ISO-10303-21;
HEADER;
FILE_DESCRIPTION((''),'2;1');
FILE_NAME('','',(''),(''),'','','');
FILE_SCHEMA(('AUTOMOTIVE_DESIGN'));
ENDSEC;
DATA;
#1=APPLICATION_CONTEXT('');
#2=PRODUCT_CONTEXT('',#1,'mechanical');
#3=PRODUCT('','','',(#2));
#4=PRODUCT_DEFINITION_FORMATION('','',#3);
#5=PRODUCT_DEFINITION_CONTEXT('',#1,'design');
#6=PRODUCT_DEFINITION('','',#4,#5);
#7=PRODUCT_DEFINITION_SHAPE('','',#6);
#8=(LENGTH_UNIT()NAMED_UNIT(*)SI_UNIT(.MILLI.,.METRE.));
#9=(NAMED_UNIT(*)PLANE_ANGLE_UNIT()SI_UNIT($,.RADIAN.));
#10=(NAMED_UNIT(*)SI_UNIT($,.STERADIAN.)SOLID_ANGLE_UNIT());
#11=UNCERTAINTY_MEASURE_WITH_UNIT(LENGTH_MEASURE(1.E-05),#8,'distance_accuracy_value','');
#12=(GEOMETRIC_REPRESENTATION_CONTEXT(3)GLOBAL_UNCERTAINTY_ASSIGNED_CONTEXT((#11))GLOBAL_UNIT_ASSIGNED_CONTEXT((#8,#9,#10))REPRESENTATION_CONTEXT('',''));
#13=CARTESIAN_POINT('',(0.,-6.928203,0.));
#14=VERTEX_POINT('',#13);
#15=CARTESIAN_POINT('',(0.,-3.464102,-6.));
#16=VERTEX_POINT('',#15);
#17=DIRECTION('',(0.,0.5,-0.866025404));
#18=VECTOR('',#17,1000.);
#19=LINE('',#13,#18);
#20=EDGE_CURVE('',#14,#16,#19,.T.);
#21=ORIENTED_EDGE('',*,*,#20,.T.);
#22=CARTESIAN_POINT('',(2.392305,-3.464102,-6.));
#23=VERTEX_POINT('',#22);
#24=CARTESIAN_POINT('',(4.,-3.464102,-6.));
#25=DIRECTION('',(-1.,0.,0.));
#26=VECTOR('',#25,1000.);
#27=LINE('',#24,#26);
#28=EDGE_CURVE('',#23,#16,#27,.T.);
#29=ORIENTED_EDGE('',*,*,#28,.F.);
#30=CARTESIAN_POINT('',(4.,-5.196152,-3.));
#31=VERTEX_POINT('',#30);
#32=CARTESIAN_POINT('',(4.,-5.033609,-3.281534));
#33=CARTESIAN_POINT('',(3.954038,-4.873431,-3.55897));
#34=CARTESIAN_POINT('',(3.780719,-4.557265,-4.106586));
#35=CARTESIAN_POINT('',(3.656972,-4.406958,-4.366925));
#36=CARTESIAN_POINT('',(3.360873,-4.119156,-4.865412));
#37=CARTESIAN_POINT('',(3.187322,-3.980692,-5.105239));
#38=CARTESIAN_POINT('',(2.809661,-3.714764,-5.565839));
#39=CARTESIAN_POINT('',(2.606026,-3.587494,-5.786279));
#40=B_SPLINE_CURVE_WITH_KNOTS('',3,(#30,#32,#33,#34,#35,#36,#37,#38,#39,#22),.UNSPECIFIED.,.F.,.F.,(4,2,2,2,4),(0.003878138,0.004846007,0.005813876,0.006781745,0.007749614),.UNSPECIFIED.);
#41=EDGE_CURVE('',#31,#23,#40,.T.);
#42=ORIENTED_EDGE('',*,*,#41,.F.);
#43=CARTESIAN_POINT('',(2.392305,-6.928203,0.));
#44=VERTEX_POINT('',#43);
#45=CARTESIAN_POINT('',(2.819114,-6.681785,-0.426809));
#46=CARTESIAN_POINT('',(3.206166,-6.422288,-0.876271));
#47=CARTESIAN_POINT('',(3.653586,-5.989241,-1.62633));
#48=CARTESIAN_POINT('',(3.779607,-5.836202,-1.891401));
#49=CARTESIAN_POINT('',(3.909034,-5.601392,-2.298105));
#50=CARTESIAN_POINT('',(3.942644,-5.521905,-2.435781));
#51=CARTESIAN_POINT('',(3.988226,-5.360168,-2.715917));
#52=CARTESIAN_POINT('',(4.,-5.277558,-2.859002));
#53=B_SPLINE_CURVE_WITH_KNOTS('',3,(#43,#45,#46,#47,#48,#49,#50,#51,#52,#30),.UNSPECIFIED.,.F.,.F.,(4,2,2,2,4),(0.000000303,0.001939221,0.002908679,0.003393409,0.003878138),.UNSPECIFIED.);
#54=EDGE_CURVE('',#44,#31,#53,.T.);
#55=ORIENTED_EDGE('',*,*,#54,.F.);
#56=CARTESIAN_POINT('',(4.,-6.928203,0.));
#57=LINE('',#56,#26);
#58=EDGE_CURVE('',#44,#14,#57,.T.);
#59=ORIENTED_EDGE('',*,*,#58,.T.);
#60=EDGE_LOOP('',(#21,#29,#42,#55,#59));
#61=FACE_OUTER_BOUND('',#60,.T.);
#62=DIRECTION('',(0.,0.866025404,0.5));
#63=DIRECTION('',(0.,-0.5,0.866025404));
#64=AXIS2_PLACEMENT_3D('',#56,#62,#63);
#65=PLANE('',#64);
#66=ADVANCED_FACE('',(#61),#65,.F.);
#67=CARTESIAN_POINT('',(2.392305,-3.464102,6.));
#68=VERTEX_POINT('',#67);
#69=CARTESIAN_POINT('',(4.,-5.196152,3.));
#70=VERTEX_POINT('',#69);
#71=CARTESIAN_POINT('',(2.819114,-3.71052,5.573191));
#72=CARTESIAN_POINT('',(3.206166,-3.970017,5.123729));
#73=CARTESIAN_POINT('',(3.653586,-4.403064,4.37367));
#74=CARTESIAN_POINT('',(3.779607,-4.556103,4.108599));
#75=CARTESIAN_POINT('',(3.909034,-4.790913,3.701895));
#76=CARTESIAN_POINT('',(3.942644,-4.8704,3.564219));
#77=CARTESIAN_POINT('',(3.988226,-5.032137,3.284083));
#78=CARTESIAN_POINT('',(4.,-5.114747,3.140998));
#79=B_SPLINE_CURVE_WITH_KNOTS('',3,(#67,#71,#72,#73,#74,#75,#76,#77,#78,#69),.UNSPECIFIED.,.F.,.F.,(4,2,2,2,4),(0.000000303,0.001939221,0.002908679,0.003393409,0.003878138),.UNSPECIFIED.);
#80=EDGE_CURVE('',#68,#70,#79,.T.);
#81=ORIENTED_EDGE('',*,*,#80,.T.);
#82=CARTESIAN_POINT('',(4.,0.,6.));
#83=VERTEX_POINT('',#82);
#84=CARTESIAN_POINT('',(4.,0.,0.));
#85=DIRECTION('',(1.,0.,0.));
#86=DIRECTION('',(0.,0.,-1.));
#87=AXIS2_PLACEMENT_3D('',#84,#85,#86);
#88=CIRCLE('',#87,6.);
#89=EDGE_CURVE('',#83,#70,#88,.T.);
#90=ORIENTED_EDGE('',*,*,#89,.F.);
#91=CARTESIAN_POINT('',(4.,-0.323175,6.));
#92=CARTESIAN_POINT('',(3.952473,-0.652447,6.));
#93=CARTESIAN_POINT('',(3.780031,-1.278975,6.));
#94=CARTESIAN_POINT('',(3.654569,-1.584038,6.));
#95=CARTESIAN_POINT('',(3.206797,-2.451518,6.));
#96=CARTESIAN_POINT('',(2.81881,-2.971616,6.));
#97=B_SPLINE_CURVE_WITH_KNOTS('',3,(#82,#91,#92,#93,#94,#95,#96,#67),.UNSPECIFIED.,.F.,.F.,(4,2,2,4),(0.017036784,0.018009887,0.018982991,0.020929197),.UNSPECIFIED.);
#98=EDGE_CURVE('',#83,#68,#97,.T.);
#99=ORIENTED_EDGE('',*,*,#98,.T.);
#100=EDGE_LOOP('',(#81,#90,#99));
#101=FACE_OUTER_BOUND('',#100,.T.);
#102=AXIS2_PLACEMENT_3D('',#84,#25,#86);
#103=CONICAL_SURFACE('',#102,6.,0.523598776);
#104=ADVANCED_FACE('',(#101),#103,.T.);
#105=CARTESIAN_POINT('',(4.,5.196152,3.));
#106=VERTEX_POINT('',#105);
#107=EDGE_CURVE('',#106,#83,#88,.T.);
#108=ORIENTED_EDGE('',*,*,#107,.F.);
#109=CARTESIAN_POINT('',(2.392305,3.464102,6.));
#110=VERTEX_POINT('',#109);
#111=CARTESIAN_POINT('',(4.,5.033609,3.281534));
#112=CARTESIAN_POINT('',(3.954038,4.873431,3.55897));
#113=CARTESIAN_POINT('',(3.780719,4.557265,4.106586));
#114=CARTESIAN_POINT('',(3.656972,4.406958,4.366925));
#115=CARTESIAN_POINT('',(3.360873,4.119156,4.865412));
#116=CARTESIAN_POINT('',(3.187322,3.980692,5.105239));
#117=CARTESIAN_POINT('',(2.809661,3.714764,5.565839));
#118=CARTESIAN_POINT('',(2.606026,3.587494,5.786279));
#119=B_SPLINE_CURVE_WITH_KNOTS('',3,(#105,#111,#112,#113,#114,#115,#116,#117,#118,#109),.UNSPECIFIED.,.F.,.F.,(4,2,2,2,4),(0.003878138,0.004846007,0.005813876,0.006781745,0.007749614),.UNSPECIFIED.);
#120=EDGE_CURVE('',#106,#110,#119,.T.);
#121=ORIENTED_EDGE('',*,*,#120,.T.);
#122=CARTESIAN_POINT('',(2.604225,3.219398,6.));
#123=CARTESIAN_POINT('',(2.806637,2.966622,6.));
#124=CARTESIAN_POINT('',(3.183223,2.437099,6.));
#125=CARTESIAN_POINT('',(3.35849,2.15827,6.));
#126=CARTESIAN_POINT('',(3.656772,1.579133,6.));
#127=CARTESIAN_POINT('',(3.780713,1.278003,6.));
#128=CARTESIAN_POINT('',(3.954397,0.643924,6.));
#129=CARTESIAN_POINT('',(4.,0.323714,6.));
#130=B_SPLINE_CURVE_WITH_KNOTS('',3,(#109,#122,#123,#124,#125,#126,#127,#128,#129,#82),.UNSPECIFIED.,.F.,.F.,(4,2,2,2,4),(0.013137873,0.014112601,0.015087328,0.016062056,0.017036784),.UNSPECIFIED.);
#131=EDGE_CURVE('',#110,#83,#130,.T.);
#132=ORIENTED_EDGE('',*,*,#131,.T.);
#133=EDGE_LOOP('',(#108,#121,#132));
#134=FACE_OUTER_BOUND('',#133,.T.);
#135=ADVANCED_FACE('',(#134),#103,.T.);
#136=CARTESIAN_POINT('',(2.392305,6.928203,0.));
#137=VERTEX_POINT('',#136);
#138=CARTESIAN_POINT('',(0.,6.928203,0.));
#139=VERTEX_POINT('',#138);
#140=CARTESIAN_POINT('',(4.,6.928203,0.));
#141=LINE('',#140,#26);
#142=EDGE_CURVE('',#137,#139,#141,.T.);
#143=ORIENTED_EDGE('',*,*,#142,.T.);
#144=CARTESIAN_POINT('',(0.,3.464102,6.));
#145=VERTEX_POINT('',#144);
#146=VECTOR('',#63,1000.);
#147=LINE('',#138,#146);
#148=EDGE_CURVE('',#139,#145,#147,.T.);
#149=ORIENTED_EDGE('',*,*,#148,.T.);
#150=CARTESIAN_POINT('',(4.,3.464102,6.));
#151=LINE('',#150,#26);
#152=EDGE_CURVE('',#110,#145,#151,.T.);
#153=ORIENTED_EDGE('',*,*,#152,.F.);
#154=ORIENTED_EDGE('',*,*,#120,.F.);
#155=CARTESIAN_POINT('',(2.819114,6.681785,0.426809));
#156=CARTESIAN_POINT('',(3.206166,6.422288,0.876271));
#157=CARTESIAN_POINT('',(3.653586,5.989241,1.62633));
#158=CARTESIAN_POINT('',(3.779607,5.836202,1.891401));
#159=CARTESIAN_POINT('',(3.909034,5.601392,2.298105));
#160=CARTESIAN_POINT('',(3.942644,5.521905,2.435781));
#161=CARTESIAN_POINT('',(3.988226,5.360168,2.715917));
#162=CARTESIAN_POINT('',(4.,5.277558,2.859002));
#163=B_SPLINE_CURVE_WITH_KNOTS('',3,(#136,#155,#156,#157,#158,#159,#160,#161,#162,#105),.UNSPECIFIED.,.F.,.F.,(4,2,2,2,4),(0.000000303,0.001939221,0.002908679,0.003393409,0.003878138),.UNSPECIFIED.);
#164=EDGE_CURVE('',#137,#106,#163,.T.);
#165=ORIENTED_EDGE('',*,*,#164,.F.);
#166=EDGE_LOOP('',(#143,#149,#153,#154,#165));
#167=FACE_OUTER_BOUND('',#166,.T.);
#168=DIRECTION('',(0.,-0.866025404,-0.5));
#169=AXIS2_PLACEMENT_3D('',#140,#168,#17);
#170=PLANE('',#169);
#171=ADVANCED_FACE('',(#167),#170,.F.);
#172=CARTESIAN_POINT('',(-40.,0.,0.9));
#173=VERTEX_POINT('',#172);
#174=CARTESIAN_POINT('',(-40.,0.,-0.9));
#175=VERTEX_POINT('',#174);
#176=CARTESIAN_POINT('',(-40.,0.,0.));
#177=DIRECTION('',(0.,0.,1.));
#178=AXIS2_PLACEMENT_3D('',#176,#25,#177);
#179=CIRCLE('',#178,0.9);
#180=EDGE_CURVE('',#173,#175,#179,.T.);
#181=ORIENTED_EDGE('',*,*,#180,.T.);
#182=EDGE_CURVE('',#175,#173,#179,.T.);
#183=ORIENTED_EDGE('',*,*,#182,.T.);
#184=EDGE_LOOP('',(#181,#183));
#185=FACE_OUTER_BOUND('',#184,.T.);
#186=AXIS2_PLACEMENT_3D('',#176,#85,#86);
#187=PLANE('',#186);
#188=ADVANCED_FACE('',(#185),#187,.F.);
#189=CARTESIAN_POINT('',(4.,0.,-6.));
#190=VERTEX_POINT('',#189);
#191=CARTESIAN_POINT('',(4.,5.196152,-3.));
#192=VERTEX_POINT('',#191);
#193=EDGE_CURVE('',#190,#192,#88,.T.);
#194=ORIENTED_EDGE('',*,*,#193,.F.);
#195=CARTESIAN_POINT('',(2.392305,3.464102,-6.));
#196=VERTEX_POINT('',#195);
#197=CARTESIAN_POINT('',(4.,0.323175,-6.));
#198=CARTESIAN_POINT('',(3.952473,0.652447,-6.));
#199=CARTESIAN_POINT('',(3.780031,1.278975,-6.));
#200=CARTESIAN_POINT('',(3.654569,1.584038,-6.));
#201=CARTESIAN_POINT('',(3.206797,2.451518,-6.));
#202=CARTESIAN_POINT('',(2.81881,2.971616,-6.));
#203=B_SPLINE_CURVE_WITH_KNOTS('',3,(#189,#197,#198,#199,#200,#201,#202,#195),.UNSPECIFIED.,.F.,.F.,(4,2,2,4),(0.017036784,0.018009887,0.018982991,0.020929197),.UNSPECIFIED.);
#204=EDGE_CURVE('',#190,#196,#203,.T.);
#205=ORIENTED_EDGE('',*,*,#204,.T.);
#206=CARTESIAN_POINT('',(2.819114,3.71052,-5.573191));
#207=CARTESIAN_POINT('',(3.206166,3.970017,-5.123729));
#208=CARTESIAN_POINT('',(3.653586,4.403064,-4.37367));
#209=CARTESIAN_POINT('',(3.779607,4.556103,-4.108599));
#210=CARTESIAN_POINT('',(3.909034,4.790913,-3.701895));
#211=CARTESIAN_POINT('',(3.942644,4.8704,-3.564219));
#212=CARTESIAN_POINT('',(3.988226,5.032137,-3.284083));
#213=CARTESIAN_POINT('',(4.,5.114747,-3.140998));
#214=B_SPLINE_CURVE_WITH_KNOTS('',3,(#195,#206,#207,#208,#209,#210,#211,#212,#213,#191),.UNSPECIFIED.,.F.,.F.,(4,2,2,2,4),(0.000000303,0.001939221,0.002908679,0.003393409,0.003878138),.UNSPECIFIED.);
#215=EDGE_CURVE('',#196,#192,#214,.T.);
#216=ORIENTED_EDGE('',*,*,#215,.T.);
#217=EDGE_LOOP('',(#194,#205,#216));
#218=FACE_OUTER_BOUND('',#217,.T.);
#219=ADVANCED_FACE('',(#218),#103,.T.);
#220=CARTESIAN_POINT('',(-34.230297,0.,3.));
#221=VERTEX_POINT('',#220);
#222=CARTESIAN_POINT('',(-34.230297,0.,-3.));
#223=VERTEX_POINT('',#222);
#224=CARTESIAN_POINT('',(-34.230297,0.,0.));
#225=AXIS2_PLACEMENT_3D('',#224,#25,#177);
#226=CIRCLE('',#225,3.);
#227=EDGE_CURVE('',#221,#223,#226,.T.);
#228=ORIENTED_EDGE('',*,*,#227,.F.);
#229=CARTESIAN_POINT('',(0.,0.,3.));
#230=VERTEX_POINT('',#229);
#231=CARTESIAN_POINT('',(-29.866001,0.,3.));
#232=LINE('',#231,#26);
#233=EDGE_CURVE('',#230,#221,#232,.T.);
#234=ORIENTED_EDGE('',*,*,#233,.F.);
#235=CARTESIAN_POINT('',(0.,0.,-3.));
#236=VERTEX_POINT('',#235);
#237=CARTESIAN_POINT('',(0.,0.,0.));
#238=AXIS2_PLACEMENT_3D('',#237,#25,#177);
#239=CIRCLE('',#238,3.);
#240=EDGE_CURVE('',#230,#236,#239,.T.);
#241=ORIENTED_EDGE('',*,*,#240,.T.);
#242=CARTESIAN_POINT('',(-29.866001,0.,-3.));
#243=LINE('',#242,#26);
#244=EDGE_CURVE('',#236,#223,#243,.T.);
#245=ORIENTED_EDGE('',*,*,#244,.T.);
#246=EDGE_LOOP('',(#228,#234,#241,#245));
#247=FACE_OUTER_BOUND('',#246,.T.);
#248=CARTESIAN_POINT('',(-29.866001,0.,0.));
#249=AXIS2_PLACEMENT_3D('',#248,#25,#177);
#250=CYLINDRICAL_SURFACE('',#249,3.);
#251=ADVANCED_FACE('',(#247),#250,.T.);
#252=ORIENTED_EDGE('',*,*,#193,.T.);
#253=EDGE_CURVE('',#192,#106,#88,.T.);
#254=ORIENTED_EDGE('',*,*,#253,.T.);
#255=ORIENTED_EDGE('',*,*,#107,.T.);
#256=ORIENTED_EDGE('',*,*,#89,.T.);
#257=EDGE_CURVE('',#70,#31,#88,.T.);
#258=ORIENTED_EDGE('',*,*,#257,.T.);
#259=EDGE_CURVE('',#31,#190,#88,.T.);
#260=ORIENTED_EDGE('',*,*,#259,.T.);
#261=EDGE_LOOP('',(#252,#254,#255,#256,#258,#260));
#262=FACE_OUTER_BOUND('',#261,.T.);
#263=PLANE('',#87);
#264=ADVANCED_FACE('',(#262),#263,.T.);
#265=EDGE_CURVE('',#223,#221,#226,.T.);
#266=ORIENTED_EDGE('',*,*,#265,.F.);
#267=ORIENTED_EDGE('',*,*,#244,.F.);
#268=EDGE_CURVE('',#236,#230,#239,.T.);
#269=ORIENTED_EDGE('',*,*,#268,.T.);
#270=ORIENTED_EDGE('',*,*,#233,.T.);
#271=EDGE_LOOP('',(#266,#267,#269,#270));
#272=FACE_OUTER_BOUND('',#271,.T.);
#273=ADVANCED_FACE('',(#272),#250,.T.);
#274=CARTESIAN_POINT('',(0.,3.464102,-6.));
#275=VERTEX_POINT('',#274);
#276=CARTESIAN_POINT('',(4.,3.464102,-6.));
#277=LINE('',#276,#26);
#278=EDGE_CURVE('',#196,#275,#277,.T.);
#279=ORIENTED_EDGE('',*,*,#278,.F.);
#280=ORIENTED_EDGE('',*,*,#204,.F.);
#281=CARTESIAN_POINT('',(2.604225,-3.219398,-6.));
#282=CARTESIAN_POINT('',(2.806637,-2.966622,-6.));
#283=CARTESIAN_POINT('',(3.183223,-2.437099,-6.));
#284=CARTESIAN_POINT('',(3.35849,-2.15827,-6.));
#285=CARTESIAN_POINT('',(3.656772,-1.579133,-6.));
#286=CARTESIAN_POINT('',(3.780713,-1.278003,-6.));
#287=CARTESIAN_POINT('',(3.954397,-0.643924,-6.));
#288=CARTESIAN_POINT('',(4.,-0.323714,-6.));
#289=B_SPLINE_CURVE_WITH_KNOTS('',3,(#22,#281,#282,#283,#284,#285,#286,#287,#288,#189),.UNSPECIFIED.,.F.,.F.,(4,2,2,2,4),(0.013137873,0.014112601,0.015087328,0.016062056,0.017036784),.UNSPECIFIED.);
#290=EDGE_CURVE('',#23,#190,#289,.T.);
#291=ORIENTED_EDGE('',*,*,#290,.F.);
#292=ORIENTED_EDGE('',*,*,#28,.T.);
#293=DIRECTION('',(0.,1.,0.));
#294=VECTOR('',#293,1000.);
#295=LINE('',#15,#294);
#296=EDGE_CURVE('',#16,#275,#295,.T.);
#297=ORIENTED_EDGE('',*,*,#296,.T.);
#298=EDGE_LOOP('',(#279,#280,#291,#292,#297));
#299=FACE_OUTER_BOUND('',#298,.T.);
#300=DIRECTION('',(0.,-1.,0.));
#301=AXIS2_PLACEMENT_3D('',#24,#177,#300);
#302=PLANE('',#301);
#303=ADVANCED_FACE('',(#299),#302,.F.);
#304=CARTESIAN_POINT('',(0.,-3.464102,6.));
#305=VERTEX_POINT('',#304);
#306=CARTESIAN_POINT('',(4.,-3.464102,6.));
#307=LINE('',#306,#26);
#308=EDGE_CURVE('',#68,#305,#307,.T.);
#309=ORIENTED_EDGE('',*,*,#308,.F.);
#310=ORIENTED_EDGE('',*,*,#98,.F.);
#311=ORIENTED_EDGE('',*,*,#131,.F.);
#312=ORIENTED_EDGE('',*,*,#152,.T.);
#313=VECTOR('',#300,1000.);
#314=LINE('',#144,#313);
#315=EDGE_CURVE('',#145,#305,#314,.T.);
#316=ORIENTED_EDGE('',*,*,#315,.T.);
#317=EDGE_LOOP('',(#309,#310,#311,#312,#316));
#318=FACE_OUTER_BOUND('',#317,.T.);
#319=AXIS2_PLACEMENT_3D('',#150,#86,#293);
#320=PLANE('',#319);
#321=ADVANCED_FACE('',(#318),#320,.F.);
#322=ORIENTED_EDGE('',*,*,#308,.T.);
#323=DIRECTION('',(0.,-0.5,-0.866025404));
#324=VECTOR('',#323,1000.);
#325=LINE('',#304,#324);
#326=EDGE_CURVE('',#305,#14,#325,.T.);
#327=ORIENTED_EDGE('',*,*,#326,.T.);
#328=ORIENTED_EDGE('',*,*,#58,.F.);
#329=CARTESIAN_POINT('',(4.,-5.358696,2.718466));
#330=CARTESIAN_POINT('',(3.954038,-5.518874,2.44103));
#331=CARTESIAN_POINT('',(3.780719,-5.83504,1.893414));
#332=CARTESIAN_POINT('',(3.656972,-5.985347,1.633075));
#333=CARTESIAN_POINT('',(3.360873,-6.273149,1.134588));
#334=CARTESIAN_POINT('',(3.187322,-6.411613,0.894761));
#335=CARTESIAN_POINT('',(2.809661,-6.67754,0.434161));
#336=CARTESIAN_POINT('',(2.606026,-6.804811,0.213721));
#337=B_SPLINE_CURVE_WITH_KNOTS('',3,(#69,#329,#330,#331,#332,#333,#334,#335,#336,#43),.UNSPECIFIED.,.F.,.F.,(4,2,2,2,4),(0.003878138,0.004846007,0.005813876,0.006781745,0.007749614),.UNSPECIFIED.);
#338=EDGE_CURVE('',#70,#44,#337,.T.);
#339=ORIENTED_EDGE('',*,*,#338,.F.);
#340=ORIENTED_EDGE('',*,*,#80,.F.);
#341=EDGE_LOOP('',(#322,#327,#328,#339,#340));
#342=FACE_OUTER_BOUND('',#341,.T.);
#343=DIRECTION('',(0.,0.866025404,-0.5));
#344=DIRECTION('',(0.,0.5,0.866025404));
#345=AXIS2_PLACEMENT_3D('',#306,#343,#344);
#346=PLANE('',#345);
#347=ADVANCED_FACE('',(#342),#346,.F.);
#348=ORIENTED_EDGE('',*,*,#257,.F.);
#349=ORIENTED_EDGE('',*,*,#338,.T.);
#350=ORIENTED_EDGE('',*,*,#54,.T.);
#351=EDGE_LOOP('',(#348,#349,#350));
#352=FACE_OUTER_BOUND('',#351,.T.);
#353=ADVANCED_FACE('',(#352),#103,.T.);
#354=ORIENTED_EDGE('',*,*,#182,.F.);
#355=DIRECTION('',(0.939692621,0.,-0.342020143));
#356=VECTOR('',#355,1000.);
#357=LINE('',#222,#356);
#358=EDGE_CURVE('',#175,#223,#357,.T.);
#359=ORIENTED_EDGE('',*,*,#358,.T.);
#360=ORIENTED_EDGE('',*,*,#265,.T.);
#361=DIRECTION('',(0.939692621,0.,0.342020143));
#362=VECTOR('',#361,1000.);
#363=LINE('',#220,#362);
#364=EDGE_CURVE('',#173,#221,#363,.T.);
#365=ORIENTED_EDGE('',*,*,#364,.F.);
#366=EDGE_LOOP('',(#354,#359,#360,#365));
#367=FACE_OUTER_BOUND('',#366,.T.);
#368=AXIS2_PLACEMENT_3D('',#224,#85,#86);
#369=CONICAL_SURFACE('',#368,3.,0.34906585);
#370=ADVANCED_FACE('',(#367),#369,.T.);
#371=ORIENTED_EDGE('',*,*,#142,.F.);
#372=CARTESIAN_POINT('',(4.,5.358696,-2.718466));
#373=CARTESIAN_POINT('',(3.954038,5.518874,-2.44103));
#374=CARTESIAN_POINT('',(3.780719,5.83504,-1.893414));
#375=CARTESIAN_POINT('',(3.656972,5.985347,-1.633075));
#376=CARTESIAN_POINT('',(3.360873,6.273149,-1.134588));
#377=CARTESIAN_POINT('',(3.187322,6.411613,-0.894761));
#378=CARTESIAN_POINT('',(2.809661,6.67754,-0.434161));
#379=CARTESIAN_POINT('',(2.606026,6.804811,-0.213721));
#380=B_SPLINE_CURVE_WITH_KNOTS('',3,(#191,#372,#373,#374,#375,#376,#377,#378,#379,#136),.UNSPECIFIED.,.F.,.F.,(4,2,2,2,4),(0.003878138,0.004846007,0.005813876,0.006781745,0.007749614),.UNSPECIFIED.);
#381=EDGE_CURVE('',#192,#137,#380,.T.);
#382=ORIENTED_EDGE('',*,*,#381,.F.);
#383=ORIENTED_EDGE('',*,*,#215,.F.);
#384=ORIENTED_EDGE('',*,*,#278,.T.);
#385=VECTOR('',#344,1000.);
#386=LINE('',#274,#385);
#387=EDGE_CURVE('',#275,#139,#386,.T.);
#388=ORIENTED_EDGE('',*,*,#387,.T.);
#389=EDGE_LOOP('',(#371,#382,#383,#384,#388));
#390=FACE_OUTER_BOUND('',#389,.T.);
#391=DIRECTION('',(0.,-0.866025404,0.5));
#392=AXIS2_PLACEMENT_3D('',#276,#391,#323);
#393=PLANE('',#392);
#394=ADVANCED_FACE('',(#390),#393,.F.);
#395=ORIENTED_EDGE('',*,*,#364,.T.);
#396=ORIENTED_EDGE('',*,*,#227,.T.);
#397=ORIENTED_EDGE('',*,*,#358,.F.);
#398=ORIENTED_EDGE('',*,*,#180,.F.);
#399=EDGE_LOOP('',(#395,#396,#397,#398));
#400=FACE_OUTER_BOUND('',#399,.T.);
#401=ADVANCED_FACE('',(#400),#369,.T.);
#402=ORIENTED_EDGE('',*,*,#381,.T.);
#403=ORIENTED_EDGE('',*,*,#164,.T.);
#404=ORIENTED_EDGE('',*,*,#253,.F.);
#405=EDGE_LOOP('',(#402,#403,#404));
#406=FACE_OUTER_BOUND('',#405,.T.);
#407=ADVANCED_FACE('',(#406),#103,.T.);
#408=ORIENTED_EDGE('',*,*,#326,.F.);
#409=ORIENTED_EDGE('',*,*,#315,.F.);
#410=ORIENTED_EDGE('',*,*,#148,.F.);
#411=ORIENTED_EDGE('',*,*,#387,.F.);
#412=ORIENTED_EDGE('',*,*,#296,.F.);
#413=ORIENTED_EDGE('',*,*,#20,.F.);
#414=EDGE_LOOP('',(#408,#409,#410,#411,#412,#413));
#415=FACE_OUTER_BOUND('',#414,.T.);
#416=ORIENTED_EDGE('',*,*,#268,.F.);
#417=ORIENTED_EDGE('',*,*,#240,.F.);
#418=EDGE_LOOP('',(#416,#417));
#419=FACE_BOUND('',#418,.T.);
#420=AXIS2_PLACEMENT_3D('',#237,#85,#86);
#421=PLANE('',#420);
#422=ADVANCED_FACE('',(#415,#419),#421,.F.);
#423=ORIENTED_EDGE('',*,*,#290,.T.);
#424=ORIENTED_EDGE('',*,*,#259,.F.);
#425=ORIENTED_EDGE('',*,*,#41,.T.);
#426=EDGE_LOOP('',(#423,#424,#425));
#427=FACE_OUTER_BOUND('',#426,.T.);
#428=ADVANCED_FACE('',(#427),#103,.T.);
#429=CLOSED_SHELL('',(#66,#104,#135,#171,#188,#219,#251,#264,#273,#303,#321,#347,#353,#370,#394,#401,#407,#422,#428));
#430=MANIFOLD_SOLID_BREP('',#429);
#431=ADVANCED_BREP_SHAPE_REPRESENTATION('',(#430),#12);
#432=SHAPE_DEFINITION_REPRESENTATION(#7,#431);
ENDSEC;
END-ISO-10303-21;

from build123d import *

# Parameters (mm, degrees)
BOSS_EXTRUDE1_DEPTH = 4
SKETCH2_OUTSIDE_W   = 22.372
SKETCH2_OUTSIDE_H   = 24.228
SKETCH2_OUTSIDE_R   = 6
CUT_EXTRUDE1_DEPTH  = 4
CUT_EXTRUDE1_DRAFT  = -30


with BuildPart() as part:
    # Sketch1 → Boss-Extrude1 (new body)
    with BuildSketch(Plane(origin=(0, 0, 0), x_dir=(0, 0, -1), z_dir=(1, 0, 0))):
        Polygon((0, -6.92820323), (6, -3.464101615), (6, 3.464101615), (0, 6.92820323), (-6, 3.464101615), (-6, -3.464101615), align=None)
    extrude(amount=BOSS_EXTRUDE1_DEPTH)


with BuildPart() as cut_extrude1_tool:
    # Sketch2 outside → Cut-Extrude1 (with draft: the straight prism first)
    with BuildSketch(Plane(origin=(4, 0, 0), x_dir=(0, 0, -1), z_dir=(1, 0, 0))):
        Rectangle(SKETCH2_OUTSIDE_W, SKETCH2_OUTSIDE_H)
        Circle(SKETCH2_OUTSIDE_R, mode=Mode.SUBTRACT)
    extrude(amount=-CUT_EXTRUDE1_DEPTH)
    # Cut-Extrude1: the draft: its side faces are tilted about the plane it starts from
    cut_extrude1_sides = [cut_extrude1_tool.faces().sort_by_distance(p)[0] for p in [
        (2, -12.114, 0),
        (2, 0, -11.186),
        (2, 12.114, 0),
        (2, 0, 11.186),
        (2, 0, 6),
    ]]
    draft(cut_extrude1_sides, Plane(origin=(4, 0, 0), x_dir=(0, 0, -1), z_dir=(1, 0, 0)), CUT_EXTRUDE1_DRAFT)


with BuildPart() as part_1:
    add(part.part)

    # Cut-Extrude1: cut by cut_extrude1_tool
    add(cut_extrude1_tool.part, mode=Mode.SUBTRACT)

    # Sketch3 → Revolve1 (revolve)
    with BuildSketch(Plane.XY, mode=Mode.PRIVATE) as revolve1_sk:
        Polygon((0, 3), (0, 0), (-40, 0), (-40, 0.9), (-34.230297419, 3), align=None)
    revolve(revolve1_sk.sketch.rotate(Axis((-29.866000922, 0, 0), (1, 0, 0)), 90), axis=Axis((-29.866000922, 0, 0), (1, 0, 0)))


solid = part_1.part
